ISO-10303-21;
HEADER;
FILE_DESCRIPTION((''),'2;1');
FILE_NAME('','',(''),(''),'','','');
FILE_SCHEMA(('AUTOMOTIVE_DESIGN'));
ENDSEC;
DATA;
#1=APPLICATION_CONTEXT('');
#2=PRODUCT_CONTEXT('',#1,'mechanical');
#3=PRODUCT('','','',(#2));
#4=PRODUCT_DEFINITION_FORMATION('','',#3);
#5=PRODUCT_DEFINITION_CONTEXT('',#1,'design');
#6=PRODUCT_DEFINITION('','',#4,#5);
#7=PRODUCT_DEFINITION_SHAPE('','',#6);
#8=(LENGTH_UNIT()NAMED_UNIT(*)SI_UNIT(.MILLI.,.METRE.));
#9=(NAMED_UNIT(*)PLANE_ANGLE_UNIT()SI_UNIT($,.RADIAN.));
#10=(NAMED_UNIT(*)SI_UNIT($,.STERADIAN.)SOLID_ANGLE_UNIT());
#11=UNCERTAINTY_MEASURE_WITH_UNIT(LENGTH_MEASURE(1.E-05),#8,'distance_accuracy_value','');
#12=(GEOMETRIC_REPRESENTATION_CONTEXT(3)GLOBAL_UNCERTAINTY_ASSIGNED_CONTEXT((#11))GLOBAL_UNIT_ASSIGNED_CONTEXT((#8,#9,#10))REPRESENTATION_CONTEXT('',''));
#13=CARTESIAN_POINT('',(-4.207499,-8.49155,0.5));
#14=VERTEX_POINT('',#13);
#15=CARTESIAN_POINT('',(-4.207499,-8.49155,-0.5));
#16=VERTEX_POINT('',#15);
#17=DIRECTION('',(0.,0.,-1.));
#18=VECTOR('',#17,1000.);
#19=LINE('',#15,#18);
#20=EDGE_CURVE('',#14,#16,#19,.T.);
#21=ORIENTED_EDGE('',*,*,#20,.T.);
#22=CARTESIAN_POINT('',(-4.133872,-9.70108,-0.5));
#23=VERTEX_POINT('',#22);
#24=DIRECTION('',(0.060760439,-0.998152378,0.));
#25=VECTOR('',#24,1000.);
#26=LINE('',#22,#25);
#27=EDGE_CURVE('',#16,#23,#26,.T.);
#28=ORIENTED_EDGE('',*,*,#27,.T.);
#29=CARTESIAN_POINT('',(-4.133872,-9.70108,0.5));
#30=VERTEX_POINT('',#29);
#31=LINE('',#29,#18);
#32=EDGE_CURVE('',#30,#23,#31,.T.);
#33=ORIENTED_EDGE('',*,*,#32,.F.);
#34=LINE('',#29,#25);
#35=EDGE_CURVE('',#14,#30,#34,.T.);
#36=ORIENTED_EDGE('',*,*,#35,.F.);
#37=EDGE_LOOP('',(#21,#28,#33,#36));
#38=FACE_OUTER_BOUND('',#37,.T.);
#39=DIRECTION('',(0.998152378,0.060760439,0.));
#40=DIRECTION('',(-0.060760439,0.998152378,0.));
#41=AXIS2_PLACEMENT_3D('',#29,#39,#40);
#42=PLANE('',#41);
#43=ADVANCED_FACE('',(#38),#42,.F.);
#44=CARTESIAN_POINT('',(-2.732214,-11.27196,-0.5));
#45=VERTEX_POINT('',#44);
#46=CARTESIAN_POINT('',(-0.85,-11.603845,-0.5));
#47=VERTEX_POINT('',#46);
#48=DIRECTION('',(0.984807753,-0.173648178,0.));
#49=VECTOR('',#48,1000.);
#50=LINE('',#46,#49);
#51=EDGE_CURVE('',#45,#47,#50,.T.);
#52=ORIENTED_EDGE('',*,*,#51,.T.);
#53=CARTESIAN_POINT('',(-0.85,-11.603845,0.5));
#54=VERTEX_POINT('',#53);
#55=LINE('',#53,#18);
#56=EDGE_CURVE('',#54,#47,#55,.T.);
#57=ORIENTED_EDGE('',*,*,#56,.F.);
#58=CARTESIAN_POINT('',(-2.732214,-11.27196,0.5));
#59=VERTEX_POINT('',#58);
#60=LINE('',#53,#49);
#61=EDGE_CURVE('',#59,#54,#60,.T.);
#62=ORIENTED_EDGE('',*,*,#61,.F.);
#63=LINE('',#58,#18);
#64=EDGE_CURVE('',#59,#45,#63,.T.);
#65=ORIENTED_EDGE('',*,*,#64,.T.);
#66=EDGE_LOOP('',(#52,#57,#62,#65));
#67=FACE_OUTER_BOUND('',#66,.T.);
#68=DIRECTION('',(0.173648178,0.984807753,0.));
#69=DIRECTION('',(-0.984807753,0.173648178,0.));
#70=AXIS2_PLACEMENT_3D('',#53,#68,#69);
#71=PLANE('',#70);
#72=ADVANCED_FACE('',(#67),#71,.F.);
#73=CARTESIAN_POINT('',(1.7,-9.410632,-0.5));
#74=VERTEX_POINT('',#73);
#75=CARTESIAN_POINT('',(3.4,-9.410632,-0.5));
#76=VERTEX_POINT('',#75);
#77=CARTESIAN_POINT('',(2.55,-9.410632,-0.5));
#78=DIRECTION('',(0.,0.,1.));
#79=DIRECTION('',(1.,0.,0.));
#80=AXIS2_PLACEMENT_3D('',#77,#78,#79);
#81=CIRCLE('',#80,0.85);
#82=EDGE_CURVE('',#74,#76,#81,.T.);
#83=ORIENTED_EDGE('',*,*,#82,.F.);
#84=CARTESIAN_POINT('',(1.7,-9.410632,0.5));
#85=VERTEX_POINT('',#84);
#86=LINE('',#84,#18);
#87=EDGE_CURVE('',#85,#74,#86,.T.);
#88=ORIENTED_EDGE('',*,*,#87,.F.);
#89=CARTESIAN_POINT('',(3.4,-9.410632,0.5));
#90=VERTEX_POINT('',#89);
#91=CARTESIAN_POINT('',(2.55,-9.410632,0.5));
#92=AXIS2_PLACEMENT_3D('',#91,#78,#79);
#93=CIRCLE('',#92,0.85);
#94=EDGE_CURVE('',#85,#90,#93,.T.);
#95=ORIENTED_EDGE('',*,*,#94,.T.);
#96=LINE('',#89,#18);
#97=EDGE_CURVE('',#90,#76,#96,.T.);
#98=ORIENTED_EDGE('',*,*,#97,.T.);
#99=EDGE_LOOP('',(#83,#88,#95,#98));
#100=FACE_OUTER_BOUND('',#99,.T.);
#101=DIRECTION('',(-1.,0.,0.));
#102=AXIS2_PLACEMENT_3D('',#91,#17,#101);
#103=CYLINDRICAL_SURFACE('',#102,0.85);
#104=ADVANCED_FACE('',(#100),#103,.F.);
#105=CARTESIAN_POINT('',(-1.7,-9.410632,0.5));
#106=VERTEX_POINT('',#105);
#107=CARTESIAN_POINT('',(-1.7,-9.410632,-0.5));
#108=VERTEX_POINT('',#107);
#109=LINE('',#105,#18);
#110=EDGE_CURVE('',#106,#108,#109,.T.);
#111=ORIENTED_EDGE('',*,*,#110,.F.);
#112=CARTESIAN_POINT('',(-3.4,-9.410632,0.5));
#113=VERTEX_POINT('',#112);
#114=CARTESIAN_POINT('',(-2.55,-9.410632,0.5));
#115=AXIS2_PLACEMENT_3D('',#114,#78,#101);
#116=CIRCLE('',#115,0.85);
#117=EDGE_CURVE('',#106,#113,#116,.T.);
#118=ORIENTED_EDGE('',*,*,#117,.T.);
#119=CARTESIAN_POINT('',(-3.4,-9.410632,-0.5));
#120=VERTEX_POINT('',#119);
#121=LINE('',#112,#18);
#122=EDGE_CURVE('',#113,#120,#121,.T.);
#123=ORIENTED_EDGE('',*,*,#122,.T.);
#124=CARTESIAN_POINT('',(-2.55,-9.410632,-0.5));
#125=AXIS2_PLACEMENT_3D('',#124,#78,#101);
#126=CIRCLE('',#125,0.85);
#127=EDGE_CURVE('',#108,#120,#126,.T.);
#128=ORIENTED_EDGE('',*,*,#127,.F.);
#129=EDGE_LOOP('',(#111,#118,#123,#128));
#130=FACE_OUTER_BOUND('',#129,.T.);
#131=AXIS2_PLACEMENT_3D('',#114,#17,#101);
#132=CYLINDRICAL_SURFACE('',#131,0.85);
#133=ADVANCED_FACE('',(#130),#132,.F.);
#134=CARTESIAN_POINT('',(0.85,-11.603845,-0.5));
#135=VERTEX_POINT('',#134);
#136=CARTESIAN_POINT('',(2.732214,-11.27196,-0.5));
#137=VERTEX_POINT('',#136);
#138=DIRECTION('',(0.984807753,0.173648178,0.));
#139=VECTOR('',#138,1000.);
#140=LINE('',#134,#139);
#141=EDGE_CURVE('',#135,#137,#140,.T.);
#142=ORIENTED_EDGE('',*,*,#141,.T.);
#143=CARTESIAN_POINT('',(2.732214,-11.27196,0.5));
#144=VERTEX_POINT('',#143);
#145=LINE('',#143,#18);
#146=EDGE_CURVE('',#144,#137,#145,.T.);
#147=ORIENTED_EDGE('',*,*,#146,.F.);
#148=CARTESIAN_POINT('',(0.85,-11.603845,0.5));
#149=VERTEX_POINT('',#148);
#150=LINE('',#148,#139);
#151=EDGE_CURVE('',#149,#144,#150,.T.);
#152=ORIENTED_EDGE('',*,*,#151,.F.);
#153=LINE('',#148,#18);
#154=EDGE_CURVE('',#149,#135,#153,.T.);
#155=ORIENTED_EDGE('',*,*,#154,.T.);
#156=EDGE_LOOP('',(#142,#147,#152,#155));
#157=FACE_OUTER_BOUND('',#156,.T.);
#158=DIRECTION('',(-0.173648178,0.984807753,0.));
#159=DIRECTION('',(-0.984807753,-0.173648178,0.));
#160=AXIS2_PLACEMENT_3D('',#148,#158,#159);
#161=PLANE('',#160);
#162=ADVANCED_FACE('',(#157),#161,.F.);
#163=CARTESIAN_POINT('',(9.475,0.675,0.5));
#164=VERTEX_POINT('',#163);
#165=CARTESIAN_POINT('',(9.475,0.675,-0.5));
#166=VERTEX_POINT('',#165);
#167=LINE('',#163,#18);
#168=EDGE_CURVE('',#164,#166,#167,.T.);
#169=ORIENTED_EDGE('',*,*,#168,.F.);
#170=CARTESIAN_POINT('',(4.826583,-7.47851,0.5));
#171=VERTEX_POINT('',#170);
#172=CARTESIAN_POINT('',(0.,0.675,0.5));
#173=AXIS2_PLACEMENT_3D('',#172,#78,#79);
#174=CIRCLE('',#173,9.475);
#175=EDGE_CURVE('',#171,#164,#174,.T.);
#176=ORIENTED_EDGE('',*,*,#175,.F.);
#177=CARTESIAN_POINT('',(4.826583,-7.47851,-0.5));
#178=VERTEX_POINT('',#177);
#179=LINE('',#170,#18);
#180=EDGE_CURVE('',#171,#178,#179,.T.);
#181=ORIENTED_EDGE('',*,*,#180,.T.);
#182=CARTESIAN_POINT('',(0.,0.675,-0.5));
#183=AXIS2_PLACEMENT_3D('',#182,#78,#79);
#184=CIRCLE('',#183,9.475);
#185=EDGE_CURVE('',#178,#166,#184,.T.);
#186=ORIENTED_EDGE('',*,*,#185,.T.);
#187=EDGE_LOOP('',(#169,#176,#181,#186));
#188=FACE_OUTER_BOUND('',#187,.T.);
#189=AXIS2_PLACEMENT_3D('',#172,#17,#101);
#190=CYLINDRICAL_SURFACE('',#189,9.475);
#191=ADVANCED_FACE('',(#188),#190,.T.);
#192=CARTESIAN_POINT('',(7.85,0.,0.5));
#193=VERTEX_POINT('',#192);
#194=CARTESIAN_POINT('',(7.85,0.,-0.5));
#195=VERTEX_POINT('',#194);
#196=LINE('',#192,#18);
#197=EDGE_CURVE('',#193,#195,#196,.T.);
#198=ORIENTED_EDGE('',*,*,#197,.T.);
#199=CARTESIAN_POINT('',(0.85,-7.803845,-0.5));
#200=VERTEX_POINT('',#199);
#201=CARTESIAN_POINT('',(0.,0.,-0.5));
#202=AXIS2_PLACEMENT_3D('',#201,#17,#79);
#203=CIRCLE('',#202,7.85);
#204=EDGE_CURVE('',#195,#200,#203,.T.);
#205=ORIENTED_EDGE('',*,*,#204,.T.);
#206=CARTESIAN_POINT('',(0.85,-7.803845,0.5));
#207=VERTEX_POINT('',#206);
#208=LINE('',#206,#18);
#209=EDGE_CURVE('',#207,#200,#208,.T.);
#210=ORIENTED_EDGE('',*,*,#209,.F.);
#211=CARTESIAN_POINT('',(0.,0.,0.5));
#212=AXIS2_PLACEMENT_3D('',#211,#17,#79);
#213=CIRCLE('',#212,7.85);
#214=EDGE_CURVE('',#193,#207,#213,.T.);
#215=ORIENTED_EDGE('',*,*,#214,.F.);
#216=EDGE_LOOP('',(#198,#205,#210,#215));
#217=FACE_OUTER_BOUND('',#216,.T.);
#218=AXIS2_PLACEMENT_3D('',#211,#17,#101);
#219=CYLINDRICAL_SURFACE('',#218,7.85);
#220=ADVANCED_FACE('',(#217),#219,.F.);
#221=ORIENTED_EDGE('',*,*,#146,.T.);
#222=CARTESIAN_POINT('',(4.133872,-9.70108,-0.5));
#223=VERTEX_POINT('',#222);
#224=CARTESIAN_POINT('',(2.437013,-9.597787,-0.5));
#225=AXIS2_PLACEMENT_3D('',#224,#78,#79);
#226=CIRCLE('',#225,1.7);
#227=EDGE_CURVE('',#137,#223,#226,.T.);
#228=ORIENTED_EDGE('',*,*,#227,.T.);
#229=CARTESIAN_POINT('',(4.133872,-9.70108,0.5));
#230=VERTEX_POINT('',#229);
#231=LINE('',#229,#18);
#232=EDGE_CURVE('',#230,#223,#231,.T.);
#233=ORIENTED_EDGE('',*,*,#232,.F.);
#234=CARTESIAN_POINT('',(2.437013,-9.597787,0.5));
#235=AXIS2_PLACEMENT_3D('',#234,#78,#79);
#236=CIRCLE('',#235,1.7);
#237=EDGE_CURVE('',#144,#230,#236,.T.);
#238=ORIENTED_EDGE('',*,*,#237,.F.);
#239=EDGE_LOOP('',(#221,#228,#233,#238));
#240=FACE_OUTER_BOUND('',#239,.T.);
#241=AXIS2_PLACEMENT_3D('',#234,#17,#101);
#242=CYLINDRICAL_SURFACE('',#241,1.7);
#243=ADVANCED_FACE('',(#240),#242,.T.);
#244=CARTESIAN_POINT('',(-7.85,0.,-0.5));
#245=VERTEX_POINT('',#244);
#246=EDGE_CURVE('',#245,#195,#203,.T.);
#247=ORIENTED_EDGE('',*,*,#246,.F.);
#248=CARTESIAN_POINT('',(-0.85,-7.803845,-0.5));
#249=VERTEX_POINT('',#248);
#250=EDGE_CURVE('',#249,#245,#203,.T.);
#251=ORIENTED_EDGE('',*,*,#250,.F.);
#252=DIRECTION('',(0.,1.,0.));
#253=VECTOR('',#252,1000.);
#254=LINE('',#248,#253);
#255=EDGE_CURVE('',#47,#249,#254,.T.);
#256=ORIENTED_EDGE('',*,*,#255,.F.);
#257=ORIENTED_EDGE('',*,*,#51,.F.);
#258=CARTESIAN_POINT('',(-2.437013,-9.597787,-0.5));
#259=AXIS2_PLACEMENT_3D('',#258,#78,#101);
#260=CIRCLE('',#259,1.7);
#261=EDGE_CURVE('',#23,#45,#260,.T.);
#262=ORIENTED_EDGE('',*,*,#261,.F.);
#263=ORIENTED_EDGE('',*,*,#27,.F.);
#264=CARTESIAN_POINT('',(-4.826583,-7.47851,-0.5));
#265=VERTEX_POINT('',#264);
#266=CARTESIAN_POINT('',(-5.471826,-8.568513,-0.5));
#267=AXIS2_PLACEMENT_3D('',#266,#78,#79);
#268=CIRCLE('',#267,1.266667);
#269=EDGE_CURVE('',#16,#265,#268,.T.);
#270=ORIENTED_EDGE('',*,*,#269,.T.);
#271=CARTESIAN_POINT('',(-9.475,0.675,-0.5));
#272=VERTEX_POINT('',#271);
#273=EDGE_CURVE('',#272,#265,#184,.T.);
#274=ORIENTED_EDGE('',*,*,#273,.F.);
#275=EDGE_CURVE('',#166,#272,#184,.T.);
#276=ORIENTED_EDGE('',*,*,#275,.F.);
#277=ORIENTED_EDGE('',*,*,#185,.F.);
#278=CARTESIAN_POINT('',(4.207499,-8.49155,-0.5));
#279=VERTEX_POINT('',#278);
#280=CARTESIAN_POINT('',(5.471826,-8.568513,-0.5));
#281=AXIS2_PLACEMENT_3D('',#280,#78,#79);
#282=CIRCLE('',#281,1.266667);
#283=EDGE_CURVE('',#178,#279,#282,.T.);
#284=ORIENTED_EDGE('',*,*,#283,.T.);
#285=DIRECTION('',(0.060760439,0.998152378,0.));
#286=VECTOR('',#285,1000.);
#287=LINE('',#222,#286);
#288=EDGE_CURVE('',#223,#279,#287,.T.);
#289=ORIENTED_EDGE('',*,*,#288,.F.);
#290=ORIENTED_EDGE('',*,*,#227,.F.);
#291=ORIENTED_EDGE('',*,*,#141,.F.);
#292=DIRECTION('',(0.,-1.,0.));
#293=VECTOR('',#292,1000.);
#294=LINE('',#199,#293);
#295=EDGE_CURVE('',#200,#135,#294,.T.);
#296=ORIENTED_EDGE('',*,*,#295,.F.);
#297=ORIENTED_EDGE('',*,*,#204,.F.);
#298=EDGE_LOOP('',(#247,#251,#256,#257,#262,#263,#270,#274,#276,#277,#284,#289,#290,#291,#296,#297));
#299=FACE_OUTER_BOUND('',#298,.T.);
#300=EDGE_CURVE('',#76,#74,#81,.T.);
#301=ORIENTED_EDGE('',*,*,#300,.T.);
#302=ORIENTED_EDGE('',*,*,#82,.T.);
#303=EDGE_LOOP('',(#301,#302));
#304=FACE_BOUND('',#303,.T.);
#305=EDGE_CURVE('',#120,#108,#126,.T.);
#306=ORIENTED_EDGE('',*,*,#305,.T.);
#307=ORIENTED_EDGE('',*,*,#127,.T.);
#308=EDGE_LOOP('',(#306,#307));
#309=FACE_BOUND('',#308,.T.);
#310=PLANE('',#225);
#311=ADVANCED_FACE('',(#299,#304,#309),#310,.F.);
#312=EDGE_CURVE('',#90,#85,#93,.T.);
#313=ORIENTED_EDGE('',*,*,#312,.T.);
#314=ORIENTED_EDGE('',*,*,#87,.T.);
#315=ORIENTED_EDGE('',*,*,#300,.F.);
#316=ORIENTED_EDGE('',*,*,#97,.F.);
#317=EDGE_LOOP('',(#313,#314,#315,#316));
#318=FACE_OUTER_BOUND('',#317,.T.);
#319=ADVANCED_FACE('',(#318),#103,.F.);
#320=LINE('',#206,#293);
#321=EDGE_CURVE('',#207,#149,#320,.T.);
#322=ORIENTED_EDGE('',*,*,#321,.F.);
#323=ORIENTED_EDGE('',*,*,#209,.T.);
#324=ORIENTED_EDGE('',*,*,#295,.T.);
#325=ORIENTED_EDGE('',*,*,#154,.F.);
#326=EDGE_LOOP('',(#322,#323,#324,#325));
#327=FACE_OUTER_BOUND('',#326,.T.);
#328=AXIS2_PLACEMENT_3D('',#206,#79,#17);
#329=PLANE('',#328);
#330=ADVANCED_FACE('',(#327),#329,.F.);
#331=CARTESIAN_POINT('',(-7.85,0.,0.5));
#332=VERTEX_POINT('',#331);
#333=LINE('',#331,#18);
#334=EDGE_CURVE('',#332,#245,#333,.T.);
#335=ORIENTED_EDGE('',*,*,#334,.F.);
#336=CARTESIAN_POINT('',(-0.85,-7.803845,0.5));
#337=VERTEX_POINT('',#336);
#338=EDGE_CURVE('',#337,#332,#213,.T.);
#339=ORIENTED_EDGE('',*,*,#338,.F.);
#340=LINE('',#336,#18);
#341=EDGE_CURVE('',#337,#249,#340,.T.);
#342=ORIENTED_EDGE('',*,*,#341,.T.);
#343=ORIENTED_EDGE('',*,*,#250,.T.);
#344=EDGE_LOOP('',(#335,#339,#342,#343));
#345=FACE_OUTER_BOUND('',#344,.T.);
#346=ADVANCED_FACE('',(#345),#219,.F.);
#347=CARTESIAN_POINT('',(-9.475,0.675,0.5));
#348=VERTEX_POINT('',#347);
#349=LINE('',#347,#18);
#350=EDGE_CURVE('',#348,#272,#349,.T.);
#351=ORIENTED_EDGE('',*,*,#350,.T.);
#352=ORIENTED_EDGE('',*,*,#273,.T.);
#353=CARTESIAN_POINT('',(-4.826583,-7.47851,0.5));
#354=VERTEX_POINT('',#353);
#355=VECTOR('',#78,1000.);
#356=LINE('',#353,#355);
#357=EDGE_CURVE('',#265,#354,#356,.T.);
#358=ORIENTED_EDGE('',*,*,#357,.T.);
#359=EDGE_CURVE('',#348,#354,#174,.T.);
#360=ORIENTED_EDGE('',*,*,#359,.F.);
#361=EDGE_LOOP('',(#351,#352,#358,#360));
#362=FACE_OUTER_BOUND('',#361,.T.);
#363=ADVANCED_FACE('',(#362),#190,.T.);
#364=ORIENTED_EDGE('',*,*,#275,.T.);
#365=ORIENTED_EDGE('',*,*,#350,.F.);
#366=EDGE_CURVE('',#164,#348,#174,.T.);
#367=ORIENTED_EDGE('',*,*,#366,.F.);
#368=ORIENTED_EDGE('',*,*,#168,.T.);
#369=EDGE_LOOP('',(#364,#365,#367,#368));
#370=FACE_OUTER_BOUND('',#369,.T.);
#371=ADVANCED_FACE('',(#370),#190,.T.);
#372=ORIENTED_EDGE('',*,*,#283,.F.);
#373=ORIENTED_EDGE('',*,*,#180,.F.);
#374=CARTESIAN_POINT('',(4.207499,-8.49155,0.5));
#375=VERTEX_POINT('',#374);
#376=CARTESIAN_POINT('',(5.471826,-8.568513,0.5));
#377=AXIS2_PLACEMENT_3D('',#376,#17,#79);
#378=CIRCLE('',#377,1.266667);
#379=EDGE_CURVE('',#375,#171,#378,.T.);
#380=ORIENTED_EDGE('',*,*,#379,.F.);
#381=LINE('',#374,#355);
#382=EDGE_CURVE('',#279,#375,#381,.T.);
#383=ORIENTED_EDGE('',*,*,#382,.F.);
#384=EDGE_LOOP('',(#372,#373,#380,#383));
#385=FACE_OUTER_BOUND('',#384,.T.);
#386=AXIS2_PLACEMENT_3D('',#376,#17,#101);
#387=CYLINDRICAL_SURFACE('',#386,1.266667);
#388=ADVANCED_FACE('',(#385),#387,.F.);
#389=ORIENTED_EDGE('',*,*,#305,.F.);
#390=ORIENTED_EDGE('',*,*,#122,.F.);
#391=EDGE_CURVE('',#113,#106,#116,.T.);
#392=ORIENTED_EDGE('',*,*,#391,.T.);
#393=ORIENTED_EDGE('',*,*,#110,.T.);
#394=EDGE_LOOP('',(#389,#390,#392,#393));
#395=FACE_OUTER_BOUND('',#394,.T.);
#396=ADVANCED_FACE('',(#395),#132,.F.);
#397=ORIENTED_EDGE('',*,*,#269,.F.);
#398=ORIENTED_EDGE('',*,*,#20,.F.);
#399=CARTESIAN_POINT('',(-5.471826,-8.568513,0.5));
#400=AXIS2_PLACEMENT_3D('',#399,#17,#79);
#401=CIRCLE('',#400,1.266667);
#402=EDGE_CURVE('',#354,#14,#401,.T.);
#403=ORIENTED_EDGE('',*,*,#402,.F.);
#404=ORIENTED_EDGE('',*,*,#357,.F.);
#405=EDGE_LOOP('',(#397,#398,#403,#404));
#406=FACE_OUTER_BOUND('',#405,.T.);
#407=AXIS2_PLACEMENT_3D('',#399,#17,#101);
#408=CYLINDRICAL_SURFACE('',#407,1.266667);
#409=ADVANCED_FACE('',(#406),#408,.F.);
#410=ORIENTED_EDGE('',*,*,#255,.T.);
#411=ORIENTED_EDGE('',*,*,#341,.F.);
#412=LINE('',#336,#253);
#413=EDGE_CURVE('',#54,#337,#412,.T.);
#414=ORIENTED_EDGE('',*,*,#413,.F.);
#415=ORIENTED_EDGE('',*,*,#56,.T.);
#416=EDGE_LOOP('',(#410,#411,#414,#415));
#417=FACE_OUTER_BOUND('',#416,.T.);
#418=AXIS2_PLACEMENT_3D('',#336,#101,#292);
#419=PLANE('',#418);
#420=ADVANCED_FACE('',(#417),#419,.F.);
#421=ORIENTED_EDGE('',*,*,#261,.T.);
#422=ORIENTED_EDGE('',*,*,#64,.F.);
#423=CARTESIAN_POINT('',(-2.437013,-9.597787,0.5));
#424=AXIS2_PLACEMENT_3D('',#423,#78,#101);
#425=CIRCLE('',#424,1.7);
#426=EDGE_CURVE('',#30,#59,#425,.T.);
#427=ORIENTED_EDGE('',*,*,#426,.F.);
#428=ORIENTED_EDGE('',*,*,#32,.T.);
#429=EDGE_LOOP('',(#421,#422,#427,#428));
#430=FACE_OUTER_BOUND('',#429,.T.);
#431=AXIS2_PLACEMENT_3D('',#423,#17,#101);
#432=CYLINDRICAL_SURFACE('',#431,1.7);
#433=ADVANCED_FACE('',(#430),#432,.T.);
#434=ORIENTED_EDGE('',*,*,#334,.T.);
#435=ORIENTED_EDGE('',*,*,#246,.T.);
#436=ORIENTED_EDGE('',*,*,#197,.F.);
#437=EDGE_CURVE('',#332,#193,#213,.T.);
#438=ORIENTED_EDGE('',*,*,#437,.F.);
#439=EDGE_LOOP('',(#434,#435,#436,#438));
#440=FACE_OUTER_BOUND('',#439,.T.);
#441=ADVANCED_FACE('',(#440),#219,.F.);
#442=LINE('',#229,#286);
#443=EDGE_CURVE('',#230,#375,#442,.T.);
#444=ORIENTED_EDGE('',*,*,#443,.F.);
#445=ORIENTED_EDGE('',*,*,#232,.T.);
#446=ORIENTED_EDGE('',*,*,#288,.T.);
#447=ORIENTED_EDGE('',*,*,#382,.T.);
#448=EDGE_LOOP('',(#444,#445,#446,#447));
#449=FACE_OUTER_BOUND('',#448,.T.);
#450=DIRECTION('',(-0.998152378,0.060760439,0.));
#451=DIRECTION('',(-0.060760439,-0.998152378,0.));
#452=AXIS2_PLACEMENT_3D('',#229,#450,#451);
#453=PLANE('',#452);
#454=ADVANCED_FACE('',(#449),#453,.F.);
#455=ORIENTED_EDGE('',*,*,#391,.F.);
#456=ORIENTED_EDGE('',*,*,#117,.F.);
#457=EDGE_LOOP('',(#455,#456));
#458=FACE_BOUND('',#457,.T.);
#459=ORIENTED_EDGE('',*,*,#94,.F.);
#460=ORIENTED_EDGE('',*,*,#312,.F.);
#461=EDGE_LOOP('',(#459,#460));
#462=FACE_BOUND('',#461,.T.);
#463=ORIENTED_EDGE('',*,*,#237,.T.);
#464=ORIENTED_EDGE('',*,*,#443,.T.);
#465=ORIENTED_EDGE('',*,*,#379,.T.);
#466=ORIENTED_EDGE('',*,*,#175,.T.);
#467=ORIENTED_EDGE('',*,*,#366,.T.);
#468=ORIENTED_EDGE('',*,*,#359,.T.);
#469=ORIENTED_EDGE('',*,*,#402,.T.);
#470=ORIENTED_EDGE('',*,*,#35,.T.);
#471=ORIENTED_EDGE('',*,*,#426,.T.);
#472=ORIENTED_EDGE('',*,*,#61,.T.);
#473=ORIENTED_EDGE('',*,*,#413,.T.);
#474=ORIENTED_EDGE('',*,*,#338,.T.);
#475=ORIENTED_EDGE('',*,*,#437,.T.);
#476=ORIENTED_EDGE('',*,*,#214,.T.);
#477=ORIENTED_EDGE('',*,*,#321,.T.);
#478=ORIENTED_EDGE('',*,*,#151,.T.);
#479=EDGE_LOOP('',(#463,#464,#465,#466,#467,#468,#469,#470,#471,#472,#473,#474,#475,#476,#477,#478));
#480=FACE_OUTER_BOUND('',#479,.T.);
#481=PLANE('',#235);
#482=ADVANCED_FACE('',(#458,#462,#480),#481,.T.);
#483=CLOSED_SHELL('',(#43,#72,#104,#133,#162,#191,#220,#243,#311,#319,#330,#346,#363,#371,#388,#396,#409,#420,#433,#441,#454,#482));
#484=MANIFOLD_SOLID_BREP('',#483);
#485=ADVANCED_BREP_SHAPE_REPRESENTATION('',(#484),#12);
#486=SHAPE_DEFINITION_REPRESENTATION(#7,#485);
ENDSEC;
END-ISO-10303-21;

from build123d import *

# Parameters (mm, degrees)
SKETCH_2_R      = 0.85
EXTRUDE_1_DEPTH = 0.5
FILLET_1_R      = 1.266666667


with BuildPart() as part:
    # 草图2 → 凸台-拉伸1 (new, symmetric)
    with BuildSketch(Plane.XY):
        with BuildLine():
            Line((4.133871572, -9.701079585), (4.25, -7.793360231))
            ThreePointArc((4.25, -7.793360231), (0, 10.15), (-4.25, -7.793360231))
            Line((-4.25, -7.793360231), (-4.133871572, -9.701079585))
            ThreePointArc((-4.133871572, -9.701079585), (-3.705473422, -10.72960262), (-2.732214432, -11.271960018))
            Line((-2.732214432, -11.271960018), (-0.85, -11.603845206))
            Line((-0.85, -11.603845206), (-0.85, -7.803845206))
            ThreePointArc((-0.85, -7.803845206), (0, 7.85), (0.85, -7.803845206))
            Line((0.85, -7.803845206), (0.85, -11.603845206))
            Line((0.85, -11.603845206), (2.732214432, -11.271960018))
            ThreePointArc((2.732214432, -11.271960018), (3.705473422, -10.72960262), (4.133871572, -9.701079585))
        make_face()
        with Locations((2.55, -9.410632285)):
            Circle(SKETCH_2_R, mode=Mode.SUBTRACT)
        with Locations(Location((-2.55, -9.410632285, 0), (0, 0, 180))):
            Circle(SKETCH_2_R, mode=Mode.SUBTRACT)
    extrude(amount=EXTRUDE_1_DEPTH, both=True)

    # 圆角1
    fillet_1_edges = [part.edges().sort_by_distance(p)[0] for p in [
        (-4.25, -7.793360231, 0),
        (4.25, -7.793360231, 0),
    ]]
    fillet(fillet_1_edges, radius=FILLET_1_R)


solid = part.part
